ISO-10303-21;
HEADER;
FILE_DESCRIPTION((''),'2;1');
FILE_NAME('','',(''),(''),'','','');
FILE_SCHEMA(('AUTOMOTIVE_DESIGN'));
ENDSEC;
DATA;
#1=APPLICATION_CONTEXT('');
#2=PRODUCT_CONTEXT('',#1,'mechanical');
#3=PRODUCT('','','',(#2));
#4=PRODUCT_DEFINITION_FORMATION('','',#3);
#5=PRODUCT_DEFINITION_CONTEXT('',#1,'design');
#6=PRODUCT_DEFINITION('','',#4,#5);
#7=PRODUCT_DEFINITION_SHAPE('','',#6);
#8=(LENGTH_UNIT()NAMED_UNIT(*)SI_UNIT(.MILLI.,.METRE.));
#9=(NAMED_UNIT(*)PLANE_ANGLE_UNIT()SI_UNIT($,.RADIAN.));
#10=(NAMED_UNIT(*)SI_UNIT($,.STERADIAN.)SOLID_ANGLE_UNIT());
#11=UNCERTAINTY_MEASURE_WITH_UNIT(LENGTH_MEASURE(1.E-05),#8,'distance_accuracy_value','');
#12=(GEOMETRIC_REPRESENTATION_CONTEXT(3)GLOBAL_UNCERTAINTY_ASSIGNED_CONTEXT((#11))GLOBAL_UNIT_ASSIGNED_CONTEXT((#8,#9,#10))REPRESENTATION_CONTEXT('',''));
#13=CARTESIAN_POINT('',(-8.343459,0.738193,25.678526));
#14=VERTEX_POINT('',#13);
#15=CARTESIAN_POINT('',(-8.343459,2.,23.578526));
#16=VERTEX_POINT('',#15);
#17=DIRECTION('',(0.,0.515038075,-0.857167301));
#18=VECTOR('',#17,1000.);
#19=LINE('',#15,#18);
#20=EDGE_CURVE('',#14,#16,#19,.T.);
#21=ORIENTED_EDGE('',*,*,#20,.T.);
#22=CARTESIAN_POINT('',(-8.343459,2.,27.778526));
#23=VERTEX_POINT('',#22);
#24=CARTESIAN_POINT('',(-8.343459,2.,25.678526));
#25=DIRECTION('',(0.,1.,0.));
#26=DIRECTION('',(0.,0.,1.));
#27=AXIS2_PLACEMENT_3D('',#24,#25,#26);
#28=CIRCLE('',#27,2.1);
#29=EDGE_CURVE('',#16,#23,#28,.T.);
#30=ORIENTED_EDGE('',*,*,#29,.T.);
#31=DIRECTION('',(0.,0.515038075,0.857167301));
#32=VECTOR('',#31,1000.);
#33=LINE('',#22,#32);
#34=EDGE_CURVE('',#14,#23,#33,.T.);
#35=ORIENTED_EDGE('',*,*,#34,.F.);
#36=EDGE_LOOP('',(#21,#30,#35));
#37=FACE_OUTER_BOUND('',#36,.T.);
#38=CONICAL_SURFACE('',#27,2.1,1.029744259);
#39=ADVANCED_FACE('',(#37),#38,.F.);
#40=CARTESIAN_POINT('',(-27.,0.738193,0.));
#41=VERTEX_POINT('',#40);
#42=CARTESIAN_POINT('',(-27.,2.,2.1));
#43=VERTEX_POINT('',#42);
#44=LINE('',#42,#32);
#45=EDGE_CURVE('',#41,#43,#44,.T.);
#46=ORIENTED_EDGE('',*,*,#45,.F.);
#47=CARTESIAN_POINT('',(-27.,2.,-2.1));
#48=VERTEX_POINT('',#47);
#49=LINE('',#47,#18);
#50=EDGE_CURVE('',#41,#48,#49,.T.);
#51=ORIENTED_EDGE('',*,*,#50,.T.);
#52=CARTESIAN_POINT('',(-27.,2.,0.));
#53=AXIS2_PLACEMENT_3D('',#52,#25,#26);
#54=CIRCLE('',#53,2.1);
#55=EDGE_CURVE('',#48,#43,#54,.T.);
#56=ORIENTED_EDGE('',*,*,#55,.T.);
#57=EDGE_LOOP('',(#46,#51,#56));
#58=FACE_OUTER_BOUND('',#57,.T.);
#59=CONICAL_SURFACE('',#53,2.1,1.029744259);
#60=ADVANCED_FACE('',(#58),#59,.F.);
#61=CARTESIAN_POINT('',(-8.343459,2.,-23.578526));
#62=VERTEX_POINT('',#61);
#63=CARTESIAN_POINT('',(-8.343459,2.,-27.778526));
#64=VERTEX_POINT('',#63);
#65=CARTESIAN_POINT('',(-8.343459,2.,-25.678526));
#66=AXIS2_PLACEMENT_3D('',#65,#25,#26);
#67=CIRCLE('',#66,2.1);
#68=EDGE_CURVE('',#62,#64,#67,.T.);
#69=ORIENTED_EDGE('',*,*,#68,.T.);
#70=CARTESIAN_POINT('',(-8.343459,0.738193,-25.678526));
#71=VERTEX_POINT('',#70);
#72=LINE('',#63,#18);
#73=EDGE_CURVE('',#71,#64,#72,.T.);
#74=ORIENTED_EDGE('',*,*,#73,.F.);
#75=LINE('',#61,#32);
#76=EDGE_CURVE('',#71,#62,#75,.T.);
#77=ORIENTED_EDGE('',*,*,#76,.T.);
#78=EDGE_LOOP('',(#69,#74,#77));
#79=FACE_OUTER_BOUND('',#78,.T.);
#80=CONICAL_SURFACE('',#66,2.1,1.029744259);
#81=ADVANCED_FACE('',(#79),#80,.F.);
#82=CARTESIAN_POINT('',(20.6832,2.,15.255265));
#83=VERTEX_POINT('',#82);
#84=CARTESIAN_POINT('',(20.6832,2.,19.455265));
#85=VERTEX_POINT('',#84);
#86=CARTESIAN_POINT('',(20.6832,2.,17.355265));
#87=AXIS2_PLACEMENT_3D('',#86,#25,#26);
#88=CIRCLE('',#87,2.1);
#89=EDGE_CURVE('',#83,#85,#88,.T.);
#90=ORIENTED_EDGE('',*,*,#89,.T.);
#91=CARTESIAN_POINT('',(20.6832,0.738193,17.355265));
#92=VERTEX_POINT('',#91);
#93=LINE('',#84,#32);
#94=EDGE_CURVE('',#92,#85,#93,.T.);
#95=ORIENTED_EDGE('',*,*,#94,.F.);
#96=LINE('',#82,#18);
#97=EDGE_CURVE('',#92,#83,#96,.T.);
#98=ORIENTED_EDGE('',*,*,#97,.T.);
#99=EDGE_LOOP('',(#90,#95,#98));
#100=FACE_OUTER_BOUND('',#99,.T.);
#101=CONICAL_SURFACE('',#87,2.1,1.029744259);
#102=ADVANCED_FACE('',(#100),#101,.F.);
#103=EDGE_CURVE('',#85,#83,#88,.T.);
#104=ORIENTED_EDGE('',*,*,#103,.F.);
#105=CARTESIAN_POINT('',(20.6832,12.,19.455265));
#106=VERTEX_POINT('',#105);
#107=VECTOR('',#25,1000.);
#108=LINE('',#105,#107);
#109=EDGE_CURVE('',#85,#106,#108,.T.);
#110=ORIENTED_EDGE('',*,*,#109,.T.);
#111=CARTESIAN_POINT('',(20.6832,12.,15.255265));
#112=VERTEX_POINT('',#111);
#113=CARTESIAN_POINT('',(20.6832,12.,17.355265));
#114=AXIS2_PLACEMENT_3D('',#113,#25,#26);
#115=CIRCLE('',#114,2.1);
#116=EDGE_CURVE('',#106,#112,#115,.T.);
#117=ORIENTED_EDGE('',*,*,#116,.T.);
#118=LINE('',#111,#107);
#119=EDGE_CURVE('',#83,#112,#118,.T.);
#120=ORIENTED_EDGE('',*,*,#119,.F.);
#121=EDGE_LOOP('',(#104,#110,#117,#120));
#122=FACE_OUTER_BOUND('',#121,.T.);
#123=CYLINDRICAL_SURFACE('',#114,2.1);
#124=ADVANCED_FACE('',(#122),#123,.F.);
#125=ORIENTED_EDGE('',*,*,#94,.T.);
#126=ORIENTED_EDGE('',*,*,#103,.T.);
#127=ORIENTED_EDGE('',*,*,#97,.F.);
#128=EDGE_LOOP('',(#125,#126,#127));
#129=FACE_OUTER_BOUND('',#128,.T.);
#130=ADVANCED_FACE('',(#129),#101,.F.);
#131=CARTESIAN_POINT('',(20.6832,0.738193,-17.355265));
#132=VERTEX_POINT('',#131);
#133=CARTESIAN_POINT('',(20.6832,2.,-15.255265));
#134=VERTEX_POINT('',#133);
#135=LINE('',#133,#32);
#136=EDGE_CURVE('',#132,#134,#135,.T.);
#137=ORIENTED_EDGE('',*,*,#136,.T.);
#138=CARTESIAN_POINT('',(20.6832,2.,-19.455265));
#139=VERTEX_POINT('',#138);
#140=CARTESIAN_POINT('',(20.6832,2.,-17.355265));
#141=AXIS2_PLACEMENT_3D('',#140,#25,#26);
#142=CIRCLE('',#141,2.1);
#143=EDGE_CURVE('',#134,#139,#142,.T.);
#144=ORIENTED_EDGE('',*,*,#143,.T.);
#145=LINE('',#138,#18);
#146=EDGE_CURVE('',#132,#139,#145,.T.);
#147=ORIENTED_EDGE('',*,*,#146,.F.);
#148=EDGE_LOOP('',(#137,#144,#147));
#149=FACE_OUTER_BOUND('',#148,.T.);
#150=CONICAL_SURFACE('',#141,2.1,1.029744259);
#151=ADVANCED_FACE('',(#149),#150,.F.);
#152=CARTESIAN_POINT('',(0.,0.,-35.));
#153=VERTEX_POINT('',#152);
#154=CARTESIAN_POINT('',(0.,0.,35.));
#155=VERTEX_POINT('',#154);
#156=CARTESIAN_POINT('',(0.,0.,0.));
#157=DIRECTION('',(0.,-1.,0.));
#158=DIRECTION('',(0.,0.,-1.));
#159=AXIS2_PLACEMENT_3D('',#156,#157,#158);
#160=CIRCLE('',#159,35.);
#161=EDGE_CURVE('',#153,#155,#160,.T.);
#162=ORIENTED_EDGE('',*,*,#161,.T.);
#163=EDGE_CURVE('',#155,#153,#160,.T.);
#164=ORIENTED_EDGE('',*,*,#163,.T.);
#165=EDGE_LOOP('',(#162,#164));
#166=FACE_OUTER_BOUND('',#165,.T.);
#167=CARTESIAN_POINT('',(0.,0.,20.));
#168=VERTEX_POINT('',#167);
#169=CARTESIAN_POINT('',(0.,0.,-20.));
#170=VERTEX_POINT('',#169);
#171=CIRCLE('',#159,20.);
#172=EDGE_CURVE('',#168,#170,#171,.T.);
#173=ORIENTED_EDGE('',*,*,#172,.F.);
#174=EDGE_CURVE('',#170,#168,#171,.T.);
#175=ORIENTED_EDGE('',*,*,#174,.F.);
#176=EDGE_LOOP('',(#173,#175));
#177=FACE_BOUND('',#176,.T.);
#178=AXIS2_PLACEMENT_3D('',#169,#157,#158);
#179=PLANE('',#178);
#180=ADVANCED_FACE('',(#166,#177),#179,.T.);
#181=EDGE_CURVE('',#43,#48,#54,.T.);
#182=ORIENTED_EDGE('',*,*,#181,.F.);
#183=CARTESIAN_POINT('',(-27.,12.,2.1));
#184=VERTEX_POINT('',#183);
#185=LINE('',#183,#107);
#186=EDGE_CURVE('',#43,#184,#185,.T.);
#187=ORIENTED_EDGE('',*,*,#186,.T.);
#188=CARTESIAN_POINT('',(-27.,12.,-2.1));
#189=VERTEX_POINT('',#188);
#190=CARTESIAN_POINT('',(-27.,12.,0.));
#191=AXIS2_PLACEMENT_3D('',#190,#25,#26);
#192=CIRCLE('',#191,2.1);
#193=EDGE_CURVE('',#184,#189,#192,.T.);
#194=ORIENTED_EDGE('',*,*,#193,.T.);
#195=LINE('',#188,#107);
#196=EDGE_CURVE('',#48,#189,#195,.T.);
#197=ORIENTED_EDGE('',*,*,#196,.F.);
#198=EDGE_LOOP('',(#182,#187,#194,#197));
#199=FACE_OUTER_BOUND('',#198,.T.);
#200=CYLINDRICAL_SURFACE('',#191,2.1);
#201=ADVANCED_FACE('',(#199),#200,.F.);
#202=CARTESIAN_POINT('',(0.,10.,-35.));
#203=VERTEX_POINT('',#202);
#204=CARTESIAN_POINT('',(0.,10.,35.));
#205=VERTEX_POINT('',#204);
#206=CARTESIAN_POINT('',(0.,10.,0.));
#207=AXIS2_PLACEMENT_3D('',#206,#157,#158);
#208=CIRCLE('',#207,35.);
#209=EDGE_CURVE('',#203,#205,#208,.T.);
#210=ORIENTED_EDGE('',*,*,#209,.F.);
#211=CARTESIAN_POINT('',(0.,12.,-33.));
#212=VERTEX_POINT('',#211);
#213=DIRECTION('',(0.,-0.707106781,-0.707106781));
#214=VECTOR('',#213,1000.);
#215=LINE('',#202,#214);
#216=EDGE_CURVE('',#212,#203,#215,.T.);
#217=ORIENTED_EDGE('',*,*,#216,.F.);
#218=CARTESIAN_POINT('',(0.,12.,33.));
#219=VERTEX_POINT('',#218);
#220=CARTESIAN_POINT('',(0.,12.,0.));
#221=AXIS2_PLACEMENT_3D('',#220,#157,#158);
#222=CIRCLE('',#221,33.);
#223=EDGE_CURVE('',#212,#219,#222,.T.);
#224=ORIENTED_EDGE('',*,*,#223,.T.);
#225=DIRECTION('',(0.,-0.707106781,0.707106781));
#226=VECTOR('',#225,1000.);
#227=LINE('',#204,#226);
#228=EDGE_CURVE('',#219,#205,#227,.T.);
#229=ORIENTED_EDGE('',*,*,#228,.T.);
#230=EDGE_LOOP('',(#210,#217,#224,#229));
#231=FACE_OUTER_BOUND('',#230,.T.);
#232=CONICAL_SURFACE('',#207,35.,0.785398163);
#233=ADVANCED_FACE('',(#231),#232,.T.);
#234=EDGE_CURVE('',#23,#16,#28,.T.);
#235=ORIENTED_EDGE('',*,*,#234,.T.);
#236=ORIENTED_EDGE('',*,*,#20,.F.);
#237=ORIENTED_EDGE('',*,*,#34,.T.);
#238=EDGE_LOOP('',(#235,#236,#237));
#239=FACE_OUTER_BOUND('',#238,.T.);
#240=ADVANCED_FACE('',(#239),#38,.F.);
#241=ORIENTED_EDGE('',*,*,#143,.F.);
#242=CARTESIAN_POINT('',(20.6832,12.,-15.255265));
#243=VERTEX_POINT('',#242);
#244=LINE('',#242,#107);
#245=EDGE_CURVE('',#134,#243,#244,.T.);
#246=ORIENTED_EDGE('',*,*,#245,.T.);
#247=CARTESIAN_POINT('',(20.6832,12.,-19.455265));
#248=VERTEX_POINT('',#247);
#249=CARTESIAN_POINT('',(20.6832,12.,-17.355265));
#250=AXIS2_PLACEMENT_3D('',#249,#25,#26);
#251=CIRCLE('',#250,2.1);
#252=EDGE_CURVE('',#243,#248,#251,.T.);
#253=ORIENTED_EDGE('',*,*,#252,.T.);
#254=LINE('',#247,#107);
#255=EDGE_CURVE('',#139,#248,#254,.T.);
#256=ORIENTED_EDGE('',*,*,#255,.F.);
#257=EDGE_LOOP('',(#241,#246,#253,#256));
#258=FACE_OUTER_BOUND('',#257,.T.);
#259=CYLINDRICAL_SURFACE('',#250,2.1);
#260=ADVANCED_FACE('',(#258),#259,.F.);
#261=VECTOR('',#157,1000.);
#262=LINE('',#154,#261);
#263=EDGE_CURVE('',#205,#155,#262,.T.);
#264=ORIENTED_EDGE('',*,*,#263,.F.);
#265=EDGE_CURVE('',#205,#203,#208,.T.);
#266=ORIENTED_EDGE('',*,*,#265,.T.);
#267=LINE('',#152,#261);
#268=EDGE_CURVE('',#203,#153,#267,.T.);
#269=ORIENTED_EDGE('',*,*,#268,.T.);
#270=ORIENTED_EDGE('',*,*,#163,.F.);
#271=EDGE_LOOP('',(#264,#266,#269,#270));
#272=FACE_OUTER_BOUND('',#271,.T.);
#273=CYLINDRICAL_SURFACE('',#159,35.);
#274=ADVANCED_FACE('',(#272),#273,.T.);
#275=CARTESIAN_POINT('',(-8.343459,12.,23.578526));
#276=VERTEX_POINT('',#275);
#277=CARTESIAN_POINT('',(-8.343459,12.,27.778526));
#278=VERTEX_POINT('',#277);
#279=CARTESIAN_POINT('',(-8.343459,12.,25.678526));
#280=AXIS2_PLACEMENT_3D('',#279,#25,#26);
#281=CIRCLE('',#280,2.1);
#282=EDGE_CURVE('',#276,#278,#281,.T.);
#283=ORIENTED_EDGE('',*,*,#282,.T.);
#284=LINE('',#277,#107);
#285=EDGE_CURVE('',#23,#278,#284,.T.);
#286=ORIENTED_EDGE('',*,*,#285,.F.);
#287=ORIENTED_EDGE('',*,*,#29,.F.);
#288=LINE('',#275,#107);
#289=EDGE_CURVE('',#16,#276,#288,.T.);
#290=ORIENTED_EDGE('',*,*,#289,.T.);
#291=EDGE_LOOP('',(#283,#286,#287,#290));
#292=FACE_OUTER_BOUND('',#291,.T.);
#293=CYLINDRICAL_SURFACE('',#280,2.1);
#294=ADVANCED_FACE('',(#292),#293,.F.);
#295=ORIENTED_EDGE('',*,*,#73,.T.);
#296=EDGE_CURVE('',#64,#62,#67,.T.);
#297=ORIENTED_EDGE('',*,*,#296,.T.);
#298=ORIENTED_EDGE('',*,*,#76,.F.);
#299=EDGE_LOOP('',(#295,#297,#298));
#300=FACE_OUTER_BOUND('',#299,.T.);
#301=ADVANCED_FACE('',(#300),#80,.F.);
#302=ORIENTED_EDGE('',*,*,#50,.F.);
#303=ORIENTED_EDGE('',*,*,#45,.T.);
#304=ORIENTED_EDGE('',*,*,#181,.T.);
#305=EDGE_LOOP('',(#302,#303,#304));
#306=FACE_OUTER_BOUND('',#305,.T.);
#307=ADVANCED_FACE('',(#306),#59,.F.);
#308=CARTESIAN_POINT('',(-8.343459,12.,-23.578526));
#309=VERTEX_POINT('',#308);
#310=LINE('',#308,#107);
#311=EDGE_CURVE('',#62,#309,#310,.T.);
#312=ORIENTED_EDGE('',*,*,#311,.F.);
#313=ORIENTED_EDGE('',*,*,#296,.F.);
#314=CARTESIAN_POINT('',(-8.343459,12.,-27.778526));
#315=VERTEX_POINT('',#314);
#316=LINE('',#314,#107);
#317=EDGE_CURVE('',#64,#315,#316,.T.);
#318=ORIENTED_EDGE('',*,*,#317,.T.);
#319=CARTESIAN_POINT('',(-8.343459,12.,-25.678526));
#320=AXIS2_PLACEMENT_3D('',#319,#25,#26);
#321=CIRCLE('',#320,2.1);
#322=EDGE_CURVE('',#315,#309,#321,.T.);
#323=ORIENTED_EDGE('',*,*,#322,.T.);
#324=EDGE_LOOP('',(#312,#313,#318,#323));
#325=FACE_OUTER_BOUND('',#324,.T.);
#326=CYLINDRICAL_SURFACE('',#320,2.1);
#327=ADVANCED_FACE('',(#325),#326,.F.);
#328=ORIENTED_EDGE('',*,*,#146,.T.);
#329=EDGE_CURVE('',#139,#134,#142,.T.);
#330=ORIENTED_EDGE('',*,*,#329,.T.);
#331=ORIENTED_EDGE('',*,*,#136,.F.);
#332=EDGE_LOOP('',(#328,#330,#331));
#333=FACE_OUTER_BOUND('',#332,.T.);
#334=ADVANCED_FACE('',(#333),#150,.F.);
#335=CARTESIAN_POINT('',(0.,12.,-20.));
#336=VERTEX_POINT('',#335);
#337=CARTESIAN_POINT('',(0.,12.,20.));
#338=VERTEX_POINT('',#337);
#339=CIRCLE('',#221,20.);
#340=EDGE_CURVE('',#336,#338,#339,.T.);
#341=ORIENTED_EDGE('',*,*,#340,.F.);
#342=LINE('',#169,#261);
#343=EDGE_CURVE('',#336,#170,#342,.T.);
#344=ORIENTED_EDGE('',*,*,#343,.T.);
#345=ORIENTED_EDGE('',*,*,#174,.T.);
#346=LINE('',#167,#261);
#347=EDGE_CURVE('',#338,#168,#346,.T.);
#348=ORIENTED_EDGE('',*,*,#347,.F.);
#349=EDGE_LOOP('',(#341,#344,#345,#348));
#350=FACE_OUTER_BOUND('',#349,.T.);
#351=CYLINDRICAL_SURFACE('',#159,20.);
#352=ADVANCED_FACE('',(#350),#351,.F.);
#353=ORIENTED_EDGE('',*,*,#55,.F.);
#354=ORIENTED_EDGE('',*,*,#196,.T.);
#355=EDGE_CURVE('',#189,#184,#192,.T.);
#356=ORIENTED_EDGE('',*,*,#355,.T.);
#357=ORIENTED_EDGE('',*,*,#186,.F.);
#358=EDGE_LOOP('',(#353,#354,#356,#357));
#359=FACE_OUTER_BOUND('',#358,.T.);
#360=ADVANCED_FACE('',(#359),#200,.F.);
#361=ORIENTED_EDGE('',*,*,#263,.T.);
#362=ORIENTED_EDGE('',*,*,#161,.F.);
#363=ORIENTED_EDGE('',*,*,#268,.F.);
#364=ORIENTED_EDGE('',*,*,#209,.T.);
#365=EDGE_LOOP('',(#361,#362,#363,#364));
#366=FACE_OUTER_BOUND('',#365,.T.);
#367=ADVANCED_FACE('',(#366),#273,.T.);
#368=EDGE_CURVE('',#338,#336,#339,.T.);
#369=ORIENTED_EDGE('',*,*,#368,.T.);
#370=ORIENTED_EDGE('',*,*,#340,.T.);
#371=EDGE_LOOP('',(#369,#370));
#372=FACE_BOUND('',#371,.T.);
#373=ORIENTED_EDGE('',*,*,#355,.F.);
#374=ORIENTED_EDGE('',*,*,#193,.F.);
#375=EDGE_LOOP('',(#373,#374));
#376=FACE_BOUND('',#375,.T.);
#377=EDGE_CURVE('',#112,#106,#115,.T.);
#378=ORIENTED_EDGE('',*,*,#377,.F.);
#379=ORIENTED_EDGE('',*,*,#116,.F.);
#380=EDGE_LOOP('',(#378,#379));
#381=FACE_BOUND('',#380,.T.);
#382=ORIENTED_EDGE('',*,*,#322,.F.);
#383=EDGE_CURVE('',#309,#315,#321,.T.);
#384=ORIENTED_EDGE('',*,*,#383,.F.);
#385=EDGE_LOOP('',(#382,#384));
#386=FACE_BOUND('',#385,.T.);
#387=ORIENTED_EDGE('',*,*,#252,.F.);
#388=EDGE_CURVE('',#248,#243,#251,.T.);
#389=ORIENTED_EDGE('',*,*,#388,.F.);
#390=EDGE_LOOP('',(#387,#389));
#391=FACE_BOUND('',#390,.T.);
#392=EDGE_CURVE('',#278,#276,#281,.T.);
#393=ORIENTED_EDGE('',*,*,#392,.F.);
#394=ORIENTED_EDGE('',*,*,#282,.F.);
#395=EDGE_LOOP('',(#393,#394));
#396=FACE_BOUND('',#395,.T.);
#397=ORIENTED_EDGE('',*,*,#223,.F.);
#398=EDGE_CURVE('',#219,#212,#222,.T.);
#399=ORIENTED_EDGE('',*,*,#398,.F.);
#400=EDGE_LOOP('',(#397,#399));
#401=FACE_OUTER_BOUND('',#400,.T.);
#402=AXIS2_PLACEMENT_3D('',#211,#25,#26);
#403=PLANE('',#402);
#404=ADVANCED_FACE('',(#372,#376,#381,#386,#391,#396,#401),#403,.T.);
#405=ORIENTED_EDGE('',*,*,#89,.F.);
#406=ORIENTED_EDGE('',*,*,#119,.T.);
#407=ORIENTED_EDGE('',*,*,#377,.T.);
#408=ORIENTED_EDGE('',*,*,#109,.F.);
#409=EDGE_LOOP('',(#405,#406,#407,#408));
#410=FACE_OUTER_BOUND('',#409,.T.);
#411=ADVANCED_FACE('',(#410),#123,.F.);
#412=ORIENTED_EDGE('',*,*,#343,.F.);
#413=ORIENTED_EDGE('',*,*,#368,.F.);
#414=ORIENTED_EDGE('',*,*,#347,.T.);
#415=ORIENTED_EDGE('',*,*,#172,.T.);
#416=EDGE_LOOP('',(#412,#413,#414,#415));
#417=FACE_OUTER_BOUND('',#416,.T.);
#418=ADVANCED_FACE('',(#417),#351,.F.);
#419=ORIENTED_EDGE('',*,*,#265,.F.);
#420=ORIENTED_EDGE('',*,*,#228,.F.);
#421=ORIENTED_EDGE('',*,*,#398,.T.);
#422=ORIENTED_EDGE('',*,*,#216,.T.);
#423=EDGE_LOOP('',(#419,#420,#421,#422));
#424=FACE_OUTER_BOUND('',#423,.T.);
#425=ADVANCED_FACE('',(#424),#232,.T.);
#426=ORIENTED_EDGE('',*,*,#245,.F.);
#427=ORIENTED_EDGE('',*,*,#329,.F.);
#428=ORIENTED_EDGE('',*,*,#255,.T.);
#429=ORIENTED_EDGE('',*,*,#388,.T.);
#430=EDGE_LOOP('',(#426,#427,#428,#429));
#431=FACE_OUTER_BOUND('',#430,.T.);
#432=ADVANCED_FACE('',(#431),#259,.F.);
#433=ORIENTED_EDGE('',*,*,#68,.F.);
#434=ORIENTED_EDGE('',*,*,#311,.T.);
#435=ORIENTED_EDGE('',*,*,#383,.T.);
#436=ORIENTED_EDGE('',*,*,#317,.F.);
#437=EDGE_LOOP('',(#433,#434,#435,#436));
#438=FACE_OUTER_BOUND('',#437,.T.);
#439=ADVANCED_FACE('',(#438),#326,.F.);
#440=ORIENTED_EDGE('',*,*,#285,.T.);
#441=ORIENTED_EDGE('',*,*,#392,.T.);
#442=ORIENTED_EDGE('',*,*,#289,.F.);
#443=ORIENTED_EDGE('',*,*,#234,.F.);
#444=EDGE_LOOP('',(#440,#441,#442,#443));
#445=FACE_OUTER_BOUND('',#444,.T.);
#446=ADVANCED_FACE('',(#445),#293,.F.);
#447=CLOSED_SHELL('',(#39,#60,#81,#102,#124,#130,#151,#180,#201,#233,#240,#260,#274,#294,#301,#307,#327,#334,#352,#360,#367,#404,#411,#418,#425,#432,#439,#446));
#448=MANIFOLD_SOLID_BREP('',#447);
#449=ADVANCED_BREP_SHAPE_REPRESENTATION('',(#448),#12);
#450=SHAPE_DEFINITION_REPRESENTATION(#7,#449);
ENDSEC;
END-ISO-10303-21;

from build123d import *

# Parameters (mm, degrees)
SKETCH2_R             = 1.75
CUT_EXTRUDE1_DEPTH    = 10
M5_TAPPED_HOLE1_D     = 4.2
M5_TAPPED_HOLE1_DEPTH = 10
M5_TAPPED_HOLE1_TIP   = 1.2618073


with BuildPart() as part:
    # Sketch1 → Revolve1 (revolve)
    with BuildSketch(Plane(origin=(0, 0, 0), x_dir=(0, 0, -1), z_dir=(1, 0, 0))):
        Polygon((35, 10), (33, 12), (20, 12), (20, 0), (35, 0), align=None)
    revolve(axis=Axis((0, 0, 0), (0, 1, 0)))

    # Sketch2 → Cut-Extrude1 (cut)
    with BuildSketch(Plane(origin=(0, 12, 0), x_dir=(1, 0, 0), z_dir=(0, 1, 0))):
        with Locations(Location((-27, 0, 0), (0, 0, 270))):
            Circle(SKETCH2_R)
        with Locations(Location((-8.343458848, 25.67852594, 0), (0, 0, 270))):
            Circle(SKETCH2_R)
        with Locations(Location((-8.343458848, -25.67852594, 0), (0, 0, 90))):
            Circle(SKETCH2_R)
        with Locations(Location((20.683199964, 17.355265462, 0), (0, 0, 270))):
            Circle(SKETCH2_R)
        with Locations(Location((20.683199964, -17.355265462, 0), (0, 0, 90))):
            Circle(SKETCH2_R)
    extrude(amount=-CUT_EXTRUDE1_DEPTH, mode=Mode.SUBTRACT)

    # M5 Tapped Hole1
    with Locations(Plane(origin=(0, 12, 0), x_dir=(1, 0, 0), z_dir=(0, 1, 0))):
        with Locations((-27, 0), (-8.343458848, 25.67852594), (20.683199964, 17.355265462), (20.683199964, -17.355265462), (-8.343458848, -25.67852594)):
            Hole(M5_TAPPED_HOLE1_D / 2, depth=M5_TAPPED_HOLE1_DEPTH)
            with Locations((0, 0, -(M5_TAPPED_HOLE1_DEPTH + M5_TAPPED_HOLE1_TIP / 2))):  # 118° drill point
                Cone(0, M5_TAPPED_HOLE1_D / 2, M5_TAPPED_HOLE1_TIP, mode=Mode.SUBTRACT)


solid = part.part
